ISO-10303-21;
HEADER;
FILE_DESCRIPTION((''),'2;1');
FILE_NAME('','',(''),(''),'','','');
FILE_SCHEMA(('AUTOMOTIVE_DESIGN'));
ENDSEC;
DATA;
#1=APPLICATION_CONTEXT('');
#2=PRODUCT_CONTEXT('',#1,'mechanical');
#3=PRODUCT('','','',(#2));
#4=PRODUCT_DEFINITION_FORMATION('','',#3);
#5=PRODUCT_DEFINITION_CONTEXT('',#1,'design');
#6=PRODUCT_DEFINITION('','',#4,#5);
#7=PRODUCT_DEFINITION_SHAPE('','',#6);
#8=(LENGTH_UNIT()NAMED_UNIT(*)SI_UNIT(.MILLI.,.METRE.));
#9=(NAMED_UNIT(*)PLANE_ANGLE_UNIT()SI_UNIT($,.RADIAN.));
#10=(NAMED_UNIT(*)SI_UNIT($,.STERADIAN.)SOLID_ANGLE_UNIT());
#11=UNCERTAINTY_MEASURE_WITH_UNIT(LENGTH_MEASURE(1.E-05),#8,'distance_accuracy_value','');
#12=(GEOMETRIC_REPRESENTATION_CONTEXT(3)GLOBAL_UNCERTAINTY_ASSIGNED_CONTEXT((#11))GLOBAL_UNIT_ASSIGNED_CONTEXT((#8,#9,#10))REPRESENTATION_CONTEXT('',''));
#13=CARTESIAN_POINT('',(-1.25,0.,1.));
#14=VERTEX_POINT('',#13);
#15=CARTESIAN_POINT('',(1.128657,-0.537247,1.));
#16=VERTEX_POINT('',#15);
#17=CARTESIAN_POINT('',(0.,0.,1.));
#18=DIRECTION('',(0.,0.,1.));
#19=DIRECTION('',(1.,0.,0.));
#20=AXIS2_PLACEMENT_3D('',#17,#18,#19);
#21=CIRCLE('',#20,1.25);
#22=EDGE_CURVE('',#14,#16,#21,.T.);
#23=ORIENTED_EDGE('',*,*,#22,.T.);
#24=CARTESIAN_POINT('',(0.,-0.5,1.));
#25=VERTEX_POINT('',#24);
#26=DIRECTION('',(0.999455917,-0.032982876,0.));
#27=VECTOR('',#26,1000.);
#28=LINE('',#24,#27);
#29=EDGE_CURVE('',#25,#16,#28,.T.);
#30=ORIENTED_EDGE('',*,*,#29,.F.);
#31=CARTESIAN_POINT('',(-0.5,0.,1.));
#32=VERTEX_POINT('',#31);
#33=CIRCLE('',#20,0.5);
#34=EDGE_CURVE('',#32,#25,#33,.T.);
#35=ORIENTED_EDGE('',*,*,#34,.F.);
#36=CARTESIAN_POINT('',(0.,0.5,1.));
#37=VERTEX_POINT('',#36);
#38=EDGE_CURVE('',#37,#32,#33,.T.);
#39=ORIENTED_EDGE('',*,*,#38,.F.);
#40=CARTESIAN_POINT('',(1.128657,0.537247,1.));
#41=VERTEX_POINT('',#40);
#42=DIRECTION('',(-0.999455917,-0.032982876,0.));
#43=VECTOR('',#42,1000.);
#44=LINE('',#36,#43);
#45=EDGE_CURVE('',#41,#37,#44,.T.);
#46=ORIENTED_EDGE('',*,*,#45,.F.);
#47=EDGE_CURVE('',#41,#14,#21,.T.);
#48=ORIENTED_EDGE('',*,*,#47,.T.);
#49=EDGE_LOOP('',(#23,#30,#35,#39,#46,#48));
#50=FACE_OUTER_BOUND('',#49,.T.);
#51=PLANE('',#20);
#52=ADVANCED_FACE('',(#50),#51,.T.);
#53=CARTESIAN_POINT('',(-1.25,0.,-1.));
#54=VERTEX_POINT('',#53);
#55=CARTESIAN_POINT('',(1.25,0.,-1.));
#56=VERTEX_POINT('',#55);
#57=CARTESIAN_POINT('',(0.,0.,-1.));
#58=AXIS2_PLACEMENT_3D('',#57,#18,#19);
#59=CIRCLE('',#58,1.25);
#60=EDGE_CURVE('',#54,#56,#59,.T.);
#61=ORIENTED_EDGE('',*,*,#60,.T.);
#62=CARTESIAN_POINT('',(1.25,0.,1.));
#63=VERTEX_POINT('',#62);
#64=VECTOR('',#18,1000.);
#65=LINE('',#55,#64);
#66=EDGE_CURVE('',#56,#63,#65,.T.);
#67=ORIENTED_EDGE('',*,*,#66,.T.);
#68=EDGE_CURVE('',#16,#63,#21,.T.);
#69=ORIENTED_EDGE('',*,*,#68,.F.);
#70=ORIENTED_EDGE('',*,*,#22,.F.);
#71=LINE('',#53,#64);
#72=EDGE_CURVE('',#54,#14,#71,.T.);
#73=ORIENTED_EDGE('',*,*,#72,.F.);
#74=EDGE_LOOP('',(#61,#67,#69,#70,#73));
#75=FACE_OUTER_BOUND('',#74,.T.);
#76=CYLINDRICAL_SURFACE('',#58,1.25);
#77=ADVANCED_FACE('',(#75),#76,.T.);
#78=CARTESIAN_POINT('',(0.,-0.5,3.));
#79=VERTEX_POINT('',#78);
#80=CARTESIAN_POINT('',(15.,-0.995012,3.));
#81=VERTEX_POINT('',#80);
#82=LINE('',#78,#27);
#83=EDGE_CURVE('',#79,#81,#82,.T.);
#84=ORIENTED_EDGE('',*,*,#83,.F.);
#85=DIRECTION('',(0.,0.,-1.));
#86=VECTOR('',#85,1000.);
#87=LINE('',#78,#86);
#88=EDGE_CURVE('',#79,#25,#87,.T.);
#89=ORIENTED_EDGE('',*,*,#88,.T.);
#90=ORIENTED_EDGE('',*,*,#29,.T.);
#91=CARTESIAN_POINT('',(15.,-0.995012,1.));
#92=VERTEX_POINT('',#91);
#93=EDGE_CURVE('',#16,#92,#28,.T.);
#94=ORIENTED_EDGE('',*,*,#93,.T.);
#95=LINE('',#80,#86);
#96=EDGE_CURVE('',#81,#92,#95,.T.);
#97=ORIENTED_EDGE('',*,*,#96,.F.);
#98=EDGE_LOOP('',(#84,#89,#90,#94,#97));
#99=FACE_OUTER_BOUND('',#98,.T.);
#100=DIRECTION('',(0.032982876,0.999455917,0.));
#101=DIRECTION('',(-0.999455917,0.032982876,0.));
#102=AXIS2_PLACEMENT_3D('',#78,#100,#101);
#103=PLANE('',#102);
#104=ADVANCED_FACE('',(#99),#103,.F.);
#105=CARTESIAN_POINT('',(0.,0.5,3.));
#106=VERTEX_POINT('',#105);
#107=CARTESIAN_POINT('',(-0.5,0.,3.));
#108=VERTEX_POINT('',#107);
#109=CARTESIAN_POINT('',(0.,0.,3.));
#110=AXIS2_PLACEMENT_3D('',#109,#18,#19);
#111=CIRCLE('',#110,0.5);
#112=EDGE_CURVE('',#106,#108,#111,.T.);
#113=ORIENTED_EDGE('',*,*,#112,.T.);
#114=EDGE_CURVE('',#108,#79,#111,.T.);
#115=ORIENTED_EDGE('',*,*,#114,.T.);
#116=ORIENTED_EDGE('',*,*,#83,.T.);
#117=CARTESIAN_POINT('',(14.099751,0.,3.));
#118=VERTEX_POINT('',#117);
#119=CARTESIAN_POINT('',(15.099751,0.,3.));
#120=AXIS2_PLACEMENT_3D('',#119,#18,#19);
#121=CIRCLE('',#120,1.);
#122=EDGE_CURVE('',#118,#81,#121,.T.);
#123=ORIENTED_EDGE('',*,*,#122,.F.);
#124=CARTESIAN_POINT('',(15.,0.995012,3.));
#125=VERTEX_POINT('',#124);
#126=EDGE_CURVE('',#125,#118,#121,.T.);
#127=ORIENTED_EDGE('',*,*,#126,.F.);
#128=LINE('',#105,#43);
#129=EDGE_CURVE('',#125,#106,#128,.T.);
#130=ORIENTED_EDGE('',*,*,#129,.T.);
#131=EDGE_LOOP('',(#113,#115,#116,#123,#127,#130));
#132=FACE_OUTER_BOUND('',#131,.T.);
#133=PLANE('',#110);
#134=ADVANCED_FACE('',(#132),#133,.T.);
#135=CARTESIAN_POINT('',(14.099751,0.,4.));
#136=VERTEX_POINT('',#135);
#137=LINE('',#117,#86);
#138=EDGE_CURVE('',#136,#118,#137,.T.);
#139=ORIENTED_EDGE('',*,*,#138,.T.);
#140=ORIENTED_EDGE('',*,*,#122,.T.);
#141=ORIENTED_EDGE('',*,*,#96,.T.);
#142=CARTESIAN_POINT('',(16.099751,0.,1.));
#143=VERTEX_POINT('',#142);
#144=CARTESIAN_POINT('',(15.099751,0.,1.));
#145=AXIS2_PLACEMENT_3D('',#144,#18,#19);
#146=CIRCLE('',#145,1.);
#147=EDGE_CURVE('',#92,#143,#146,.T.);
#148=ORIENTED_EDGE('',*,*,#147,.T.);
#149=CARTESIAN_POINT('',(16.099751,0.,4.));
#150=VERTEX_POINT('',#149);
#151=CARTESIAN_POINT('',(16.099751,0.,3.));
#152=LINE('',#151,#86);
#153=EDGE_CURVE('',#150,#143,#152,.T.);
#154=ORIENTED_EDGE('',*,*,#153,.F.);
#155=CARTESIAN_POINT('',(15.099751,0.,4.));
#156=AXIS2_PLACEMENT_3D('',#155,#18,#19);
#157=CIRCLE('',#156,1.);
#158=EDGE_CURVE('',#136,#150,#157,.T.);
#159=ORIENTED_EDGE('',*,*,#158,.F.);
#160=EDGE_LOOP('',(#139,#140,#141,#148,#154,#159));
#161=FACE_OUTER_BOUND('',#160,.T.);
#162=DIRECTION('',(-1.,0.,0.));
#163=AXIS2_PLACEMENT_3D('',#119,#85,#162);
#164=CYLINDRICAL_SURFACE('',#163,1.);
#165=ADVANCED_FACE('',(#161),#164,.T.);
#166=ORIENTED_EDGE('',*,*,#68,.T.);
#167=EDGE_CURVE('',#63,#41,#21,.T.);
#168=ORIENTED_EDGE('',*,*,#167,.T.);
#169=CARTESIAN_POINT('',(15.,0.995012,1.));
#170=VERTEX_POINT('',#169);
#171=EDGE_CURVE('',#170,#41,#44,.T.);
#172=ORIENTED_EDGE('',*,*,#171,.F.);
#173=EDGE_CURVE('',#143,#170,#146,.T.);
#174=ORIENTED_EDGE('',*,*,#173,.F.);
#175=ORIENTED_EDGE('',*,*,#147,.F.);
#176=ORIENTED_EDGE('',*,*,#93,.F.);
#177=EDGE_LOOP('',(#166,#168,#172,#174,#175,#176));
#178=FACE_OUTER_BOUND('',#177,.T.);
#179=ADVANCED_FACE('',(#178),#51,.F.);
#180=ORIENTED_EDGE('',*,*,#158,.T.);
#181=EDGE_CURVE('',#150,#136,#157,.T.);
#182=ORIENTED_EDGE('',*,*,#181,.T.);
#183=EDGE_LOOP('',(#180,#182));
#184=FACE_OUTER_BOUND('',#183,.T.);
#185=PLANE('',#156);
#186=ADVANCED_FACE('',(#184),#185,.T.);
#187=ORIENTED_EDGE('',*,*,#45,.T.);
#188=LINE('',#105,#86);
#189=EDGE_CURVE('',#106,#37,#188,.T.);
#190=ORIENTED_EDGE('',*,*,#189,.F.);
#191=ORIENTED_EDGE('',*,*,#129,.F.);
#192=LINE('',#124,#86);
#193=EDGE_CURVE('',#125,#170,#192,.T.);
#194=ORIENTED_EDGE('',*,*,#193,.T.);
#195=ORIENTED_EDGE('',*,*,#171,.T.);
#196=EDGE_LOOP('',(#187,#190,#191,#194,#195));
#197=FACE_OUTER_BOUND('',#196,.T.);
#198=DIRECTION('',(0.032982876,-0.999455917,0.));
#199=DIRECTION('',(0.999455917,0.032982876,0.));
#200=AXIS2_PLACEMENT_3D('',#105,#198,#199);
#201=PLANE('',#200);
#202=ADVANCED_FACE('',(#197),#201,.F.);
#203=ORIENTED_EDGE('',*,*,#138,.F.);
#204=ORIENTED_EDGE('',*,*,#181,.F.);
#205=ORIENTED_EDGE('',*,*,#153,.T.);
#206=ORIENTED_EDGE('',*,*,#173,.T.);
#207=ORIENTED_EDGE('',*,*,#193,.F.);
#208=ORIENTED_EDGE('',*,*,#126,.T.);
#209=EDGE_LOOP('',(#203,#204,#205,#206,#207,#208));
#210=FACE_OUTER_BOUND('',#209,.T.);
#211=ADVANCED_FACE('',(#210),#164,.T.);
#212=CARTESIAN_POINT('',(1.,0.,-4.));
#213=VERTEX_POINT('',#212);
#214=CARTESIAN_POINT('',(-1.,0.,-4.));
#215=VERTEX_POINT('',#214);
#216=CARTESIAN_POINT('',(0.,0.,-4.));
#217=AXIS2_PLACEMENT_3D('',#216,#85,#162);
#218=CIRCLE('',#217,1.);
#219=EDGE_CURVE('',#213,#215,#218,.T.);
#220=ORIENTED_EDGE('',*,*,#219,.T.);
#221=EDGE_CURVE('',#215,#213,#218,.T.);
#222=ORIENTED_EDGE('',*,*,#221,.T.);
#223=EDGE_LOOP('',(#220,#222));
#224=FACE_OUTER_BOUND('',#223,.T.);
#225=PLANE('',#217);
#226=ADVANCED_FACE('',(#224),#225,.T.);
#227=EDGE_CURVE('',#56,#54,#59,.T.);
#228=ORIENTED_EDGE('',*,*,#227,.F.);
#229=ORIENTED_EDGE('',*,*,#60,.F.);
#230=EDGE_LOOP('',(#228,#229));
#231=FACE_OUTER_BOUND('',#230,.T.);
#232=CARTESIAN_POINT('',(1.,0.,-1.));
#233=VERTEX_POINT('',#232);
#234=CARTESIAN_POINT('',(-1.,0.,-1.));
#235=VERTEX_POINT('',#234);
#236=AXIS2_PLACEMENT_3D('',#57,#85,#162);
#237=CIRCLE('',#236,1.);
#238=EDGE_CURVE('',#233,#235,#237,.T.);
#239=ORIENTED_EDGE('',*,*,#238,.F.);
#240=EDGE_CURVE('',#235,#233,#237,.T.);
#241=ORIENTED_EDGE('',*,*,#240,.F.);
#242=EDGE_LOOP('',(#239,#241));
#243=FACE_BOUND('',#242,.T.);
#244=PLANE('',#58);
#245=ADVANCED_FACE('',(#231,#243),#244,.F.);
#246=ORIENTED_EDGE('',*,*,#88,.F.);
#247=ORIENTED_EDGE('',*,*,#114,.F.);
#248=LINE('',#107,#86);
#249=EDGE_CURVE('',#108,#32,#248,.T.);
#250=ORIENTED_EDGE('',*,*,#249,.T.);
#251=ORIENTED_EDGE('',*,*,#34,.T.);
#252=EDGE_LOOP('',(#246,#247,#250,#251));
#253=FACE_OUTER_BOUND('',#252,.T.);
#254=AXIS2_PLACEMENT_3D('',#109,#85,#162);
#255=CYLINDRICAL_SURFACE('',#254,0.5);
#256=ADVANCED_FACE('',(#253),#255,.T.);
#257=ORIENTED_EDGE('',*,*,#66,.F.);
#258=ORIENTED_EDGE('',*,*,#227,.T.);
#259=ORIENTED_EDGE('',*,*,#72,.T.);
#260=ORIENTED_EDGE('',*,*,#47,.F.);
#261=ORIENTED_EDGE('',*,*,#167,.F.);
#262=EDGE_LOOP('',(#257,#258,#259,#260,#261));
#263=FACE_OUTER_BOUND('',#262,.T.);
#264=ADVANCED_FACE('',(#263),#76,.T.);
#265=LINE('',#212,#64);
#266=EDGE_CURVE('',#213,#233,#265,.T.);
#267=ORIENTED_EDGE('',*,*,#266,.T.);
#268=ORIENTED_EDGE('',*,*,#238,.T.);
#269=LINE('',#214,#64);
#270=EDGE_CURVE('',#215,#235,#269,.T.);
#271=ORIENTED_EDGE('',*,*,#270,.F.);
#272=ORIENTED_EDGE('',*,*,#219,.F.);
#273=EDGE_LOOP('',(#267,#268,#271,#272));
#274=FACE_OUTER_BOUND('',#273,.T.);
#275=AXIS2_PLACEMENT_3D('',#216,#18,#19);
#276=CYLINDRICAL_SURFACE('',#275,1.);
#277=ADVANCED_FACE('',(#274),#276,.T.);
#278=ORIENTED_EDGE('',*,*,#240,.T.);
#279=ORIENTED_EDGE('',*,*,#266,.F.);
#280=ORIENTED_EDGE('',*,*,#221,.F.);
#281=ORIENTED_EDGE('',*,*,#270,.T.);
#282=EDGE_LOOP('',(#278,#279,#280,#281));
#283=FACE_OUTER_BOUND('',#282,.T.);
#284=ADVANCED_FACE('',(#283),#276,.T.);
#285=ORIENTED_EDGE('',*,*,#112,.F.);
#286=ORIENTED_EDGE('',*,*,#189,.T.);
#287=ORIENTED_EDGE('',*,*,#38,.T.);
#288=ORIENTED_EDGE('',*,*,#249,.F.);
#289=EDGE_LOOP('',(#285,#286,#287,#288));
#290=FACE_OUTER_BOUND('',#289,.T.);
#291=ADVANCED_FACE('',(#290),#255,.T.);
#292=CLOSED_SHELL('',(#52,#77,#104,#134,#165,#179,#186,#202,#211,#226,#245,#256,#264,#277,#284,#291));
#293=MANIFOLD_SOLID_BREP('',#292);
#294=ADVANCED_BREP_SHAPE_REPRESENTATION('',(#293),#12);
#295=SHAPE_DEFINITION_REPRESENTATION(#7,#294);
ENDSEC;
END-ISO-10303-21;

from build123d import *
from build123d.topology import SkipClean

# Parameters (mm, degrees)
SKETCH1_R           = 1.25
BOSS_EXTRUDE1_DEPTH = 1
SKETCH2_R           = 1
BOSS_EXTRUDE2_DEPTH = 1
BOSS_EXTRUDE3_DEPTH = 2
SKETCH4_R           = 1
BOSS_EXTRUDE4_DEPTH = 1
BOSS_EXTRUDE5_START = 1
SKETCH5_R           = 1.25
BOSS_EXTRUDE5_DEPTH = 1
SKETCH6_R           = 1
BOSS_EXTRUDE6_DEPTH = 3


with BuildPart() as part:
    # Sketch1 → Boss-Extrude1 (new body)
    with BuildSketch(Plane.XY):
        Circle(SKETCH1_R)
    extrude(amount=-BOSS_EXTRUDE1_DEPTH)

    # Sketch2 → Boss-Extrude2 (add)
    with BuildSketch(Plane.XY):
        Circle(SKETCH2_R)
    extrude(amount=BOSS_EXTRUDE2_DEPTH)

    # Sketch3 → Boss-Extrude3 (add)
    with BuildSketch(Plane.XY.offset(1)):
        with BuildLine():
            Line((0, 0.5), (15, 0.995012469))
            ThreePointArc((15, 0.995012469), (16.099750623, 0), (15, -0.995012469))
            Line((15, -0.995012469), (0, -0.5))
            ThreePointArc((0, -0.5), (-0.5, 0), (0, 0.5))
        make_face()
    extrude(amount=BOSS_EXTRUDE3_DEPTH)

    # Sketch4 → Boss-Extrude4 (add)
    with SkipClean():  # the faces are left unmerged after this step: merging them gives an invalid solid
        with BuildSketch(Plane.XY.offset(3)):
            with Locations(Location((15.099750623, 0, 0), (0, 0, 264.275189548))):
                Circle(SKETCH4_R)
        extrude(amount=BOSS_EXTRUDE4_DEPTH)

    # Sketch5 → Boss-Extrude5 (add)
    with SkipClean():  # the faces are left unmerged after this step: merging them gives an invalid solid
        with BuildSketch(Plane.XY.offset(BOSS_EXTRUDE5_START)):
            Circle(SKETCH5_R)
        extrude(amount=-BOSS_EXTRUDE5_DEPTH)

    # Sketch6 → Boss-Extrude6 (add)
    with SkipClean():  # the faces are left unmerged after this step: merging them gives an invalid solid
        with BuildSketch(Plane(origin=(0, 0, -1), x_dir=(-1, 0, 0), z_dir=(0, 0, -1))):
            Circle(SKETCH6_R)
        extrude(amount=BOSS_EXTRUDE6_DEPTH)


solid = part.part
